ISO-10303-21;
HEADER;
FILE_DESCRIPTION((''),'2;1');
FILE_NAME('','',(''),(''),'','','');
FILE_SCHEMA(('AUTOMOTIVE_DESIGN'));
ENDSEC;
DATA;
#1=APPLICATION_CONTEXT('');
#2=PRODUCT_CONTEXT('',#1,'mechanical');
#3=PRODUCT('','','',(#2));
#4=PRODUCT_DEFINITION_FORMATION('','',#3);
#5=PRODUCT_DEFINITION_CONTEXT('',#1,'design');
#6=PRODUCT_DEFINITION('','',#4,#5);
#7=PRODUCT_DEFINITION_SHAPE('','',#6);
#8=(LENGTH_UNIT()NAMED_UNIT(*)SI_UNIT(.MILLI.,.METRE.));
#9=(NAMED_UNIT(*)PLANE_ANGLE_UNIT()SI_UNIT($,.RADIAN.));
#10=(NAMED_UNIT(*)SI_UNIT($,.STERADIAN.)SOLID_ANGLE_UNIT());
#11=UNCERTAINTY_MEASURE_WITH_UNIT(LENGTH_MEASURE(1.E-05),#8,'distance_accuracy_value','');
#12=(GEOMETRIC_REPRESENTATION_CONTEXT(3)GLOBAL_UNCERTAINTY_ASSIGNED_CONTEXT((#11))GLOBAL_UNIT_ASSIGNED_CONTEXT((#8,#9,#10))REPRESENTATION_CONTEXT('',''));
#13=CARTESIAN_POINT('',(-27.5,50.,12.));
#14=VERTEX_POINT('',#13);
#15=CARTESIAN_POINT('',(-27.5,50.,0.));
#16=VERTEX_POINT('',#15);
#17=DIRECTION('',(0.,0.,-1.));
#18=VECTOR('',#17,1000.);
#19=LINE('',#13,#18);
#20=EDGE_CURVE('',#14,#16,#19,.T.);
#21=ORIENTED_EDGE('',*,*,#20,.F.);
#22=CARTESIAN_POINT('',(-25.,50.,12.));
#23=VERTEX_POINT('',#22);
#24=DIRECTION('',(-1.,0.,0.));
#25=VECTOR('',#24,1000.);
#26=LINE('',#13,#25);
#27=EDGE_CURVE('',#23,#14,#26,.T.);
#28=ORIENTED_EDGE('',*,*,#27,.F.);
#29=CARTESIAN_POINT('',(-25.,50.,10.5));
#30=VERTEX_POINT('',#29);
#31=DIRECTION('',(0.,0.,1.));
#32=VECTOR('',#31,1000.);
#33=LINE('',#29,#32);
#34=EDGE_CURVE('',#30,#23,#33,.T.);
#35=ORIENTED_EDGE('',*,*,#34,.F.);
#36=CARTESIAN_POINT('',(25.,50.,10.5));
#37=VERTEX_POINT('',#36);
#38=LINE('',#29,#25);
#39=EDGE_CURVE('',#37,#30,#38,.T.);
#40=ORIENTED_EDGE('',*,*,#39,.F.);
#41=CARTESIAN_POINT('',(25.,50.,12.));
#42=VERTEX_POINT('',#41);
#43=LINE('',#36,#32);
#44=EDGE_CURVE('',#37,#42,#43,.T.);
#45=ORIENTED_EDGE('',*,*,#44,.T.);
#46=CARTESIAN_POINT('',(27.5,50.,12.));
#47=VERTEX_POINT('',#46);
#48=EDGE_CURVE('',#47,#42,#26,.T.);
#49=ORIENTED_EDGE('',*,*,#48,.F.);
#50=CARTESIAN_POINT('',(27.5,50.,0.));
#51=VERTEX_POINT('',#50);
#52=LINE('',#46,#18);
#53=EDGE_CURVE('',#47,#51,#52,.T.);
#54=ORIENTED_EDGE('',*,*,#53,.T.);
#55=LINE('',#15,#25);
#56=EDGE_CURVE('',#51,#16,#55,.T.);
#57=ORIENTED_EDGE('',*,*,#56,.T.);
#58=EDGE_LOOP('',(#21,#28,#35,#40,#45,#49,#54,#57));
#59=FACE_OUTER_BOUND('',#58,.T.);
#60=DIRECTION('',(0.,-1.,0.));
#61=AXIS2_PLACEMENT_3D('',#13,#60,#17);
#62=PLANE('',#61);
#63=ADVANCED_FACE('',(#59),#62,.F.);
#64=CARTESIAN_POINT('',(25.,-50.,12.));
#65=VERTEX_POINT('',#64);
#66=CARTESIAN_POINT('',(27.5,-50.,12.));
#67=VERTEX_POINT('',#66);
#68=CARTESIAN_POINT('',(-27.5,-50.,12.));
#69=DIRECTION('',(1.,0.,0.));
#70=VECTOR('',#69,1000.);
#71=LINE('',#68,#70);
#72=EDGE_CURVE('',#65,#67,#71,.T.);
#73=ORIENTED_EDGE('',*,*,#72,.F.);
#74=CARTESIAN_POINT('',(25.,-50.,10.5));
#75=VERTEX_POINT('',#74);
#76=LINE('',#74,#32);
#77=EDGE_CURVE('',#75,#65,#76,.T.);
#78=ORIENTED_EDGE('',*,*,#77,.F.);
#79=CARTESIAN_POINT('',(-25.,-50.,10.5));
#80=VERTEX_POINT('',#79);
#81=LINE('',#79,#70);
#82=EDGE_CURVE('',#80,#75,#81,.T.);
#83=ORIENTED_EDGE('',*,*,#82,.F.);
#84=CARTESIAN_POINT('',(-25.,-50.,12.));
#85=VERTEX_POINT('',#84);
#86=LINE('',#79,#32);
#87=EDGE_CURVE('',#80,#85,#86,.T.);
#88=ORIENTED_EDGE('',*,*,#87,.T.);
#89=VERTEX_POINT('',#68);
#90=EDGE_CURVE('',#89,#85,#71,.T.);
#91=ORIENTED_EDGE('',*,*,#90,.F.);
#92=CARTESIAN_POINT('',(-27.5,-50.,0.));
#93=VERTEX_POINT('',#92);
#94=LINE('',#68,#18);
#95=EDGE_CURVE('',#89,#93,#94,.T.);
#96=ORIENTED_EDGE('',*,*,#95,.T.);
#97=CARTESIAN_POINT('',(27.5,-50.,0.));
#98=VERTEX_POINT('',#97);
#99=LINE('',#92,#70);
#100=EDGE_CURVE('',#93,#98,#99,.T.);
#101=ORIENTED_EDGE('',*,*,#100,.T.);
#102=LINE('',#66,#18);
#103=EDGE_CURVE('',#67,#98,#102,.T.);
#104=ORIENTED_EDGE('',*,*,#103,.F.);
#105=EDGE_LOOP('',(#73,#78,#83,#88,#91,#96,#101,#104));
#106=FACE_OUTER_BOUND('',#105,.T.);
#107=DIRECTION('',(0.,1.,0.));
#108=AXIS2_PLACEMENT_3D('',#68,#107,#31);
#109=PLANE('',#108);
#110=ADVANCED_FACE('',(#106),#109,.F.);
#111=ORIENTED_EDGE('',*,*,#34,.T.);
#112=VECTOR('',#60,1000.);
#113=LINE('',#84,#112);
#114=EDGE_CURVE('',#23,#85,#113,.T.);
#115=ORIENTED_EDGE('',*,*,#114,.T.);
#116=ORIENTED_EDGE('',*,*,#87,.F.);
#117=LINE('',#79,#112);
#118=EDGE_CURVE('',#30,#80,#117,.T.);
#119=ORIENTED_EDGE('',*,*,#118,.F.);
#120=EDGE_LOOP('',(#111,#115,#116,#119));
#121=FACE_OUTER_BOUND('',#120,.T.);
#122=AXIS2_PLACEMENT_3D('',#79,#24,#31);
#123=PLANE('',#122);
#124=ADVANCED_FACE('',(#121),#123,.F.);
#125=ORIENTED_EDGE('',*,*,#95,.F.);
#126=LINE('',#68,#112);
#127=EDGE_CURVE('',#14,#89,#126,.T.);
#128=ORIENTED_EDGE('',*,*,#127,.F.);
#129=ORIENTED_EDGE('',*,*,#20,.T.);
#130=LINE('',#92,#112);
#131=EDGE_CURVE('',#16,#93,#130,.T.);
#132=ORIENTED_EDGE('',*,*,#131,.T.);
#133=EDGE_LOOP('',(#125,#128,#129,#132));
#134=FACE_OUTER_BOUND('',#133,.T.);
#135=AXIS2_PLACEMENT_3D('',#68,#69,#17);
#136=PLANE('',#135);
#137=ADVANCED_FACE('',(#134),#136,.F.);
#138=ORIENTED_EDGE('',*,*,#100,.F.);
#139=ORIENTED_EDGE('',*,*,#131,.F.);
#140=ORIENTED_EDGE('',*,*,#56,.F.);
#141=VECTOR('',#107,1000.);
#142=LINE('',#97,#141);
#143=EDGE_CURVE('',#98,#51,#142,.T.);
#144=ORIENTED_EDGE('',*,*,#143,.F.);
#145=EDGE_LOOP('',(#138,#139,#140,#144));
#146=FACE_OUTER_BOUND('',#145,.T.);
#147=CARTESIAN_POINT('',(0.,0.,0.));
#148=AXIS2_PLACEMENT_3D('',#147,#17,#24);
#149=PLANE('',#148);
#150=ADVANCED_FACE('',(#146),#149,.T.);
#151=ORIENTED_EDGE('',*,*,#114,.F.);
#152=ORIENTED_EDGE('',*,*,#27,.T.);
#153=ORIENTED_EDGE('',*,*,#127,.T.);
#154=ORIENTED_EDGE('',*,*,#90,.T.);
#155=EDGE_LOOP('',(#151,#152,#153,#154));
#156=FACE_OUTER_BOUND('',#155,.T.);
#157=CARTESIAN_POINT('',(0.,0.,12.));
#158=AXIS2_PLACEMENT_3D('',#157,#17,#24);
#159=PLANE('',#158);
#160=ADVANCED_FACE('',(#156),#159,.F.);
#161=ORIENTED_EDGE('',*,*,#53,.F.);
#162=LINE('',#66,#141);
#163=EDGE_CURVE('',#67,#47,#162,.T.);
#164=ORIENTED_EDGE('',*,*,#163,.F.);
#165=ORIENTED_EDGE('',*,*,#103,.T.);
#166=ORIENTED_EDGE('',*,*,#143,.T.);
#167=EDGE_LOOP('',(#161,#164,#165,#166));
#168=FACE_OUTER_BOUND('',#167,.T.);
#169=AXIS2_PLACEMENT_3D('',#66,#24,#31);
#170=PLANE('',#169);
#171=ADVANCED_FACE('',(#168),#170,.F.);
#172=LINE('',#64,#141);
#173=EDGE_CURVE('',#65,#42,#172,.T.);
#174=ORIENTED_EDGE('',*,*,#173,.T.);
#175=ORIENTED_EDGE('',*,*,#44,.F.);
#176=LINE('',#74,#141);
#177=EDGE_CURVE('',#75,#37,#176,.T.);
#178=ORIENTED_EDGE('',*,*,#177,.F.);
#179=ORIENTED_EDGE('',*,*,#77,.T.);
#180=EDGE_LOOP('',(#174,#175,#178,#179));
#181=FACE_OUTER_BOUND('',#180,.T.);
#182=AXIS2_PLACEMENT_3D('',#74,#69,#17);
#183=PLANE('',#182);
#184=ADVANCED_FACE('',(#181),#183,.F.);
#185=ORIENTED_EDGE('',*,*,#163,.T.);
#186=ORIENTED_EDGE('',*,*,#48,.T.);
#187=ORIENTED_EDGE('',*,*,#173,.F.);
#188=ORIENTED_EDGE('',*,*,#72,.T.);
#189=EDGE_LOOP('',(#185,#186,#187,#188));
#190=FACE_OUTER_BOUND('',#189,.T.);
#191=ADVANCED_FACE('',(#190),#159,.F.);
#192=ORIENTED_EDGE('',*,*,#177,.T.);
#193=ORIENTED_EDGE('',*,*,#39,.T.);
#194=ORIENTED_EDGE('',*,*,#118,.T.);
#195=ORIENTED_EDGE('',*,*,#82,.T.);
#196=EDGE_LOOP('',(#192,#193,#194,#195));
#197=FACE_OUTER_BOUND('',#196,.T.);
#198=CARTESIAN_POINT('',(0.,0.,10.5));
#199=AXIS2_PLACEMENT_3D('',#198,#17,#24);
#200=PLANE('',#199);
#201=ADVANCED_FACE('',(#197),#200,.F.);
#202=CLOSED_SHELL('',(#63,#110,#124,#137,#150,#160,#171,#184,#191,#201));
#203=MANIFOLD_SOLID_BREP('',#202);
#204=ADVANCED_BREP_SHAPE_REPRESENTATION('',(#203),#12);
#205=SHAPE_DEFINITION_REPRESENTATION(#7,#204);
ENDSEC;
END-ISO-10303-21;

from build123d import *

# Parameters (mm, degrees)
SKETCH_1_W          = 55
SKETCH_1_H          = 100
EXTRUDE_1_DEPTH     = 12
SKETCH_2_W          = 50
SKETCH_2_H          = 100
CUT_EXTRUDE_1_DEPTH = 1.5


with BuildPart() as part:
    # 草图1 → 凸台-拉伸1 (new body)
    with BuildSketch(Plane.XY):
        Rectangle(SKETCH_1_W, SKETCH_1_H)
    extrude(amount=EXTRUDE_1_DEPTH)

    # 草图2 → 切除-拉伸1 (cut)
    with BuildSketch(Plane.XY.offset(12)):
        Rectangle(SKETCH_2_W, SKETCH_2_H)
    extrude(amount=-CUT_EXTRUDE_1_DEPTH, mode=Mode.SUBTRACT)


solid = part.part
